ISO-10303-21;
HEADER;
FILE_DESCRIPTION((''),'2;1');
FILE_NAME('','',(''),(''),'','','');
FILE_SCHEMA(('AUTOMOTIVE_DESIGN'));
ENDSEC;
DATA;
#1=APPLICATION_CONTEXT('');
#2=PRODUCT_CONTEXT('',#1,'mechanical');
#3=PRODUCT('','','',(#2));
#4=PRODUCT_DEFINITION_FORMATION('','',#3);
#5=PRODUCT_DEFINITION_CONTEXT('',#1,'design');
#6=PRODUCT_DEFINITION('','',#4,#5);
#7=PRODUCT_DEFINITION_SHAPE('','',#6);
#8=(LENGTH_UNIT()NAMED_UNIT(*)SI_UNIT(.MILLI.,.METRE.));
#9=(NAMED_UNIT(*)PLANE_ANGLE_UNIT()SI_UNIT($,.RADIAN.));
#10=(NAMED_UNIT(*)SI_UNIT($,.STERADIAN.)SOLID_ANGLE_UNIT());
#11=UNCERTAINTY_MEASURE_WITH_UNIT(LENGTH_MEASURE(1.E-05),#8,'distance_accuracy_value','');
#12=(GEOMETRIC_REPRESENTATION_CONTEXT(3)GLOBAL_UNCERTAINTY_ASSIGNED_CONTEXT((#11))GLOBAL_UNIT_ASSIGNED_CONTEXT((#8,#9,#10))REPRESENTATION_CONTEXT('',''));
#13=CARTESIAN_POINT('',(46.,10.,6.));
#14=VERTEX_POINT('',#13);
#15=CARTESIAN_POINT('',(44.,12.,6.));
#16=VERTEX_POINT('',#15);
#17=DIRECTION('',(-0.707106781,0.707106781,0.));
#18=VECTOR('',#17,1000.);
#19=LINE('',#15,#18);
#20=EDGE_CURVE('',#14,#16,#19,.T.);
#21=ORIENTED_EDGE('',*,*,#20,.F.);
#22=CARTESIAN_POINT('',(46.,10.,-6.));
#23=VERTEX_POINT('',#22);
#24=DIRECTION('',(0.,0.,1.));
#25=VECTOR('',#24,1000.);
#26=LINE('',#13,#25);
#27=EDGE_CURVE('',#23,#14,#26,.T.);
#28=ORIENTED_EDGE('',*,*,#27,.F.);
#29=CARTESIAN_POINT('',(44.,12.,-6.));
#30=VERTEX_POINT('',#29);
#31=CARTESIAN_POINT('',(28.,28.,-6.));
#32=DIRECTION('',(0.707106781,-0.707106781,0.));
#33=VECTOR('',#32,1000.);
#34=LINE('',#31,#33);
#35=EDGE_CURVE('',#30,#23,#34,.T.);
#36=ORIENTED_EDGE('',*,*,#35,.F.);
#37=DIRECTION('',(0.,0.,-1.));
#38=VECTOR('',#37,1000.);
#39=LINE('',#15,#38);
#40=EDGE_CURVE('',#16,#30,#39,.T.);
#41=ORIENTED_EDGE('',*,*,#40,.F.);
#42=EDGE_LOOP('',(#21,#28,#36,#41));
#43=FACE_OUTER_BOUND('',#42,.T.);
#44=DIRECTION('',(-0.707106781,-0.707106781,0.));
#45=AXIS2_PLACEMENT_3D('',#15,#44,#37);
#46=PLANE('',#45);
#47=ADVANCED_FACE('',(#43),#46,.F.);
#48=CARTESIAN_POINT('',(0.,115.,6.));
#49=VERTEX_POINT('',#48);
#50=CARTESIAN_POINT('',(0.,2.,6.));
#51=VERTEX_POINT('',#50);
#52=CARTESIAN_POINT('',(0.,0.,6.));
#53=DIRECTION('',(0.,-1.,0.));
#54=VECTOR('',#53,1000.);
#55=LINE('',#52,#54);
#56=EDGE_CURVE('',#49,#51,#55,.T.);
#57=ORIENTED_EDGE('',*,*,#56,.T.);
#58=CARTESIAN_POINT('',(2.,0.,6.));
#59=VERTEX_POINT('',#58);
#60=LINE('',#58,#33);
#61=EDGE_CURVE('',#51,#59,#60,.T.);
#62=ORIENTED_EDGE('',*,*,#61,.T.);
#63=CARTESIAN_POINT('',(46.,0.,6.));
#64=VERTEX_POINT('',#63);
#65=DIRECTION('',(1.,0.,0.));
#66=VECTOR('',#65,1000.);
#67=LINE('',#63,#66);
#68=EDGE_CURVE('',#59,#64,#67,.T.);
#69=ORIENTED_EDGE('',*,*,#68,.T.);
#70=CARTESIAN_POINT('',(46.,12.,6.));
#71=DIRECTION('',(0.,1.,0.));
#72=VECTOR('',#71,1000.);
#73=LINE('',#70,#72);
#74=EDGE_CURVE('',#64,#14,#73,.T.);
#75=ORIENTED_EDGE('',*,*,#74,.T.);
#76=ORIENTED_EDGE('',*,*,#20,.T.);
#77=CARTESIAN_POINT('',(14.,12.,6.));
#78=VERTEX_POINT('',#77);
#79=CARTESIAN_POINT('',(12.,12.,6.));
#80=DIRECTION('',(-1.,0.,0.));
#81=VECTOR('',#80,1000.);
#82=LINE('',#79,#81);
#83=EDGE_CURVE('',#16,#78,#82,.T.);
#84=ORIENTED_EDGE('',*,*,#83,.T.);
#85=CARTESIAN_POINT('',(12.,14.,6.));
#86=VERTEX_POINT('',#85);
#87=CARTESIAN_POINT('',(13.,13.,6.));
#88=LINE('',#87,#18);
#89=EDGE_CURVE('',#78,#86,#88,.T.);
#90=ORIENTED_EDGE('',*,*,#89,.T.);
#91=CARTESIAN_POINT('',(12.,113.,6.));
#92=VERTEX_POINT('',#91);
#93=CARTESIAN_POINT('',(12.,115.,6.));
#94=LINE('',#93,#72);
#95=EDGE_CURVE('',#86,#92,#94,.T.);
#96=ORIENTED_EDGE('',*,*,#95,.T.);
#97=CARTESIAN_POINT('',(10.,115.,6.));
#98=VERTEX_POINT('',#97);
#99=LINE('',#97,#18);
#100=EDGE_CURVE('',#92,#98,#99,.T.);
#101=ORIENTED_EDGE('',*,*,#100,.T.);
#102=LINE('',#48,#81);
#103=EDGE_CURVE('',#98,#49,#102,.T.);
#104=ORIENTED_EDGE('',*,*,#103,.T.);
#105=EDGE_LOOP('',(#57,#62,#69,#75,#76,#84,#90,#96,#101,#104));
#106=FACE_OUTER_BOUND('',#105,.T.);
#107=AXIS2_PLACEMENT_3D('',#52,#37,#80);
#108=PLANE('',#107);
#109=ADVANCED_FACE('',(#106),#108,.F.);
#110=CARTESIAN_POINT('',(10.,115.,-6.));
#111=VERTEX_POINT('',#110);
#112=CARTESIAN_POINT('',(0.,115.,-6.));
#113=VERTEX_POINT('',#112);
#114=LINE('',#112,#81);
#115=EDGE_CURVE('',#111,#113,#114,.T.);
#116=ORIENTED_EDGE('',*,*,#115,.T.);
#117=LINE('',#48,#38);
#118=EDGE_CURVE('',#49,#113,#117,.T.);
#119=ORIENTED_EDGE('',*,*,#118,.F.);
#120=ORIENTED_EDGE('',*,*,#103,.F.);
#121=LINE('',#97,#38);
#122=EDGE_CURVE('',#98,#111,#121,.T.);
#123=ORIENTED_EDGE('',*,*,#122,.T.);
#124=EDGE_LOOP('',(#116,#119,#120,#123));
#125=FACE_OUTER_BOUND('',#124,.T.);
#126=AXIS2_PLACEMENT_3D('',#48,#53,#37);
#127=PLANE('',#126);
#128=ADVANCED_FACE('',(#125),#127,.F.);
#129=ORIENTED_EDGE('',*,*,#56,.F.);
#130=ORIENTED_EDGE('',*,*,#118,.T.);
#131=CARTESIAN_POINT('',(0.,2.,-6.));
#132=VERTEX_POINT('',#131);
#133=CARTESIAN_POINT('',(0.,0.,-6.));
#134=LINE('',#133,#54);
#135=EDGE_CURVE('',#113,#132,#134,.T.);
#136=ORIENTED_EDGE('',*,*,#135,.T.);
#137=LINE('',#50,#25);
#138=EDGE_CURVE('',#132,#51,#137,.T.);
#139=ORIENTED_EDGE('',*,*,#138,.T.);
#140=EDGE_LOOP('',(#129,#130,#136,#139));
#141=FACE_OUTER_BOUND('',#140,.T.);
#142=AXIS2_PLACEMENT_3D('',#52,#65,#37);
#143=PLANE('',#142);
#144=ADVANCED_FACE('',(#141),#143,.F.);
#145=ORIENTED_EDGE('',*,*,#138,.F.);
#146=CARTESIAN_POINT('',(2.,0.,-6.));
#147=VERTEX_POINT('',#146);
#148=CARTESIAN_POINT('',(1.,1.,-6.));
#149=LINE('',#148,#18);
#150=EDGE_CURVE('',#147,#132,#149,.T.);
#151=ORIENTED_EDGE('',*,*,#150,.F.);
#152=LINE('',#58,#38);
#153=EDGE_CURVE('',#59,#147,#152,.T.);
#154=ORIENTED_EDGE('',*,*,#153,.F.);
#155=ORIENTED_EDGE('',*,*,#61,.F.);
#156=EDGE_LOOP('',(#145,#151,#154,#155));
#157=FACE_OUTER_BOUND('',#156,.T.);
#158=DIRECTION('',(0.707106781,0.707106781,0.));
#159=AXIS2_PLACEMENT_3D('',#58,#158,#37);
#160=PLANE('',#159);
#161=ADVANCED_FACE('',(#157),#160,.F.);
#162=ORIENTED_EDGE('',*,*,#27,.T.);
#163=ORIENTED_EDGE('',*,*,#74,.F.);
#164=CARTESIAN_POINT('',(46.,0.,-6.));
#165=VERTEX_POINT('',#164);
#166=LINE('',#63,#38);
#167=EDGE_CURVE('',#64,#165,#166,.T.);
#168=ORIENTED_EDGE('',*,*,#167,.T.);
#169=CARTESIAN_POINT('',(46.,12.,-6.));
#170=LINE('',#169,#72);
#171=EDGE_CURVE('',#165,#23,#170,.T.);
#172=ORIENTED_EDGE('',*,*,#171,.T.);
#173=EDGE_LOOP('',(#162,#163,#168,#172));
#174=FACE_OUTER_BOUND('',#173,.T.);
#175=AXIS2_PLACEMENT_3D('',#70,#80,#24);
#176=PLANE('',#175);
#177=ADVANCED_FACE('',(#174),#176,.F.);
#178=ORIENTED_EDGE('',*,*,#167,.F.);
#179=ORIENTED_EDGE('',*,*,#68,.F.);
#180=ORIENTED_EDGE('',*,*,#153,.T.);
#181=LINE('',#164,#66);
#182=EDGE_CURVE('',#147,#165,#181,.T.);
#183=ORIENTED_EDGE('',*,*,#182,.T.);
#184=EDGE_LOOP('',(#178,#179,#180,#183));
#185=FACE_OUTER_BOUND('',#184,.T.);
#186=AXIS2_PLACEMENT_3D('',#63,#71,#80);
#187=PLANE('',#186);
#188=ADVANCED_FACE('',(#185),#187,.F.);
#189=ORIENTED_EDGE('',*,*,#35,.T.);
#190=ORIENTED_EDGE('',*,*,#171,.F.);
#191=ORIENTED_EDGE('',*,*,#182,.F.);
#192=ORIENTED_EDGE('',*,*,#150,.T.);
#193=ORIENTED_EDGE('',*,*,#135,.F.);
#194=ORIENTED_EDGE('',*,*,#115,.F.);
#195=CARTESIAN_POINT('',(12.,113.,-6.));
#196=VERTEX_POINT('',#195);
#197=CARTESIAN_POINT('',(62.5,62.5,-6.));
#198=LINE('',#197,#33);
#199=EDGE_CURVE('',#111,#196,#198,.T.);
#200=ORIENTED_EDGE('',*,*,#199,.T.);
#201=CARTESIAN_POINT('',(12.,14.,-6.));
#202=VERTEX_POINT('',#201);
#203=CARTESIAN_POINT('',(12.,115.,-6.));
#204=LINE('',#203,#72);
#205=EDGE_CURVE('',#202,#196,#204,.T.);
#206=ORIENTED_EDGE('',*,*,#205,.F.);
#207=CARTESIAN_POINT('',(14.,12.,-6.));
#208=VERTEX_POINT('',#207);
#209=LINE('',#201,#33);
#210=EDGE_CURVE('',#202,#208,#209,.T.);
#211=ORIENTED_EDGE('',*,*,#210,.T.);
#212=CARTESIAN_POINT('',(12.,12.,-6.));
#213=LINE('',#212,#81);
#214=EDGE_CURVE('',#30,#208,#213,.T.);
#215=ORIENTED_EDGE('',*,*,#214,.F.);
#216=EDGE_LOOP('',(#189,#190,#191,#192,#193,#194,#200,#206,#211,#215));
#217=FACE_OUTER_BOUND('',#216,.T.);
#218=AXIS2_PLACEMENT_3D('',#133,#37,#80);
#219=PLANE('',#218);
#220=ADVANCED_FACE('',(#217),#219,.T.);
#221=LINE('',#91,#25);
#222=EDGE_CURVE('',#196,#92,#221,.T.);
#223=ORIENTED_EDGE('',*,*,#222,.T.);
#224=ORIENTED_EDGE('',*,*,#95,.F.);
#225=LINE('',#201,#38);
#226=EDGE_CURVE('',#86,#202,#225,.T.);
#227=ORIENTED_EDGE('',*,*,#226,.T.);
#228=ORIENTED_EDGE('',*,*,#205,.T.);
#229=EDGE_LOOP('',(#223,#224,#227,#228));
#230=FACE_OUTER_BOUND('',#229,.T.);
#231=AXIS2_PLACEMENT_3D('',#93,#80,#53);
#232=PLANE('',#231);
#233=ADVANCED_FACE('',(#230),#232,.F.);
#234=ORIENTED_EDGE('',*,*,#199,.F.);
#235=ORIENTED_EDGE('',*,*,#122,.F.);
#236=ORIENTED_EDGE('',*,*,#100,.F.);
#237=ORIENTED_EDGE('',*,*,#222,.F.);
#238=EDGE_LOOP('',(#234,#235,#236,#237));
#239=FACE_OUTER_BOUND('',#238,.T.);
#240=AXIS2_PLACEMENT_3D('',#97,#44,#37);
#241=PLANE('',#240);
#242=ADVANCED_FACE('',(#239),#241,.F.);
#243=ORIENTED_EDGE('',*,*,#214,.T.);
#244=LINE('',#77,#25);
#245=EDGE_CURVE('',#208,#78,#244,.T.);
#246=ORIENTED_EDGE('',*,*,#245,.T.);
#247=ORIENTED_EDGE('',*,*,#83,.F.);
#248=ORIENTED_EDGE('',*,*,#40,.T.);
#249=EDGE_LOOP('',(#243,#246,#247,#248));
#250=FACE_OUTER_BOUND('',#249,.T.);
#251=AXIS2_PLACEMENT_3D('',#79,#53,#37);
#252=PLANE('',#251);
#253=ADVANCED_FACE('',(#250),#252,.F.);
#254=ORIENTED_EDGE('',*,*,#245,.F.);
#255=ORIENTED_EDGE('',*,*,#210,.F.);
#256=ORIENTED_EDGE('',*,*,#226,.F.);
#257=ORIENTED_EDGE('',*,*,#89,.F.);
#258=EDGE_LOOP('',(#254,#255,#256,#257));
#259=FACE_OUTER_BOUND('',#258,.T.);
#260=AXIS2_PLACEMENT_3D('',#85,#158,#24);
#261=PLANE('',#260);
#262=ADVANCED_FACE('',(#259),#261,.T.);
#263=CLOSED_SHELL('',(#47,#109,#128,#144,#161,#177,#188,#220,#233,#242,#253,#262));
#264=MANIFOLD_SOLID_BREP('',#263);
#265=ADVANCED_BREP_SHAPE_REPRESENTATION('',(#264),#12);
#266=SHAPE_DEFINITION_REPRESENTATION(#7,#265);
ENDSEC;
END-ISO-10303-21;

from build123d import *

# Parameters (mm, degrees)
EXTRUDE_1_DEPTH = 6
CHAMFER_1_SIZE  = 2
CHAMFER_2_SIZE  = 2
CHAMFER_3_SIZE  = 2


with BuildPart() as part:
    # 草图1 → 凸台-拉伸1 (new, symmetric)
    with BuildSketch(Plane.XY):
        Polygon((0, 0), (0, 115), (12, 115), (12, 12), (46, 12), (46, 0), align=None)
    extrude(amount=EXTRUDE_1_DEPTH, both=True)

    # 倒角1
    chamfer_1_edges = [part.edges().sort_by_distance(p)[0] for p in [
        (12, 12, 0),
    ]]
    chamfer(chamfer_1_edges, length=CHAMFER_1_SIZE)

    # 倒角2
    chamfer_2_edges = [part.edges().sort_by_distance(p)[0] for p in [
        (0, 0, 0),
    ]]
    chamfer(chamfer_2_edges, length=CHAMFER_2_SIZE)

    # 倒角3
    chamfer_3_edges = [part.edges().sort_by_distance(p)[0] for p in [
        (12, 115, 0),
        (46, 12, 0),
    ]]
    chamfer(chamfer_3_edges, length=CHAMFER_3_SIZE)


solid = part.part
